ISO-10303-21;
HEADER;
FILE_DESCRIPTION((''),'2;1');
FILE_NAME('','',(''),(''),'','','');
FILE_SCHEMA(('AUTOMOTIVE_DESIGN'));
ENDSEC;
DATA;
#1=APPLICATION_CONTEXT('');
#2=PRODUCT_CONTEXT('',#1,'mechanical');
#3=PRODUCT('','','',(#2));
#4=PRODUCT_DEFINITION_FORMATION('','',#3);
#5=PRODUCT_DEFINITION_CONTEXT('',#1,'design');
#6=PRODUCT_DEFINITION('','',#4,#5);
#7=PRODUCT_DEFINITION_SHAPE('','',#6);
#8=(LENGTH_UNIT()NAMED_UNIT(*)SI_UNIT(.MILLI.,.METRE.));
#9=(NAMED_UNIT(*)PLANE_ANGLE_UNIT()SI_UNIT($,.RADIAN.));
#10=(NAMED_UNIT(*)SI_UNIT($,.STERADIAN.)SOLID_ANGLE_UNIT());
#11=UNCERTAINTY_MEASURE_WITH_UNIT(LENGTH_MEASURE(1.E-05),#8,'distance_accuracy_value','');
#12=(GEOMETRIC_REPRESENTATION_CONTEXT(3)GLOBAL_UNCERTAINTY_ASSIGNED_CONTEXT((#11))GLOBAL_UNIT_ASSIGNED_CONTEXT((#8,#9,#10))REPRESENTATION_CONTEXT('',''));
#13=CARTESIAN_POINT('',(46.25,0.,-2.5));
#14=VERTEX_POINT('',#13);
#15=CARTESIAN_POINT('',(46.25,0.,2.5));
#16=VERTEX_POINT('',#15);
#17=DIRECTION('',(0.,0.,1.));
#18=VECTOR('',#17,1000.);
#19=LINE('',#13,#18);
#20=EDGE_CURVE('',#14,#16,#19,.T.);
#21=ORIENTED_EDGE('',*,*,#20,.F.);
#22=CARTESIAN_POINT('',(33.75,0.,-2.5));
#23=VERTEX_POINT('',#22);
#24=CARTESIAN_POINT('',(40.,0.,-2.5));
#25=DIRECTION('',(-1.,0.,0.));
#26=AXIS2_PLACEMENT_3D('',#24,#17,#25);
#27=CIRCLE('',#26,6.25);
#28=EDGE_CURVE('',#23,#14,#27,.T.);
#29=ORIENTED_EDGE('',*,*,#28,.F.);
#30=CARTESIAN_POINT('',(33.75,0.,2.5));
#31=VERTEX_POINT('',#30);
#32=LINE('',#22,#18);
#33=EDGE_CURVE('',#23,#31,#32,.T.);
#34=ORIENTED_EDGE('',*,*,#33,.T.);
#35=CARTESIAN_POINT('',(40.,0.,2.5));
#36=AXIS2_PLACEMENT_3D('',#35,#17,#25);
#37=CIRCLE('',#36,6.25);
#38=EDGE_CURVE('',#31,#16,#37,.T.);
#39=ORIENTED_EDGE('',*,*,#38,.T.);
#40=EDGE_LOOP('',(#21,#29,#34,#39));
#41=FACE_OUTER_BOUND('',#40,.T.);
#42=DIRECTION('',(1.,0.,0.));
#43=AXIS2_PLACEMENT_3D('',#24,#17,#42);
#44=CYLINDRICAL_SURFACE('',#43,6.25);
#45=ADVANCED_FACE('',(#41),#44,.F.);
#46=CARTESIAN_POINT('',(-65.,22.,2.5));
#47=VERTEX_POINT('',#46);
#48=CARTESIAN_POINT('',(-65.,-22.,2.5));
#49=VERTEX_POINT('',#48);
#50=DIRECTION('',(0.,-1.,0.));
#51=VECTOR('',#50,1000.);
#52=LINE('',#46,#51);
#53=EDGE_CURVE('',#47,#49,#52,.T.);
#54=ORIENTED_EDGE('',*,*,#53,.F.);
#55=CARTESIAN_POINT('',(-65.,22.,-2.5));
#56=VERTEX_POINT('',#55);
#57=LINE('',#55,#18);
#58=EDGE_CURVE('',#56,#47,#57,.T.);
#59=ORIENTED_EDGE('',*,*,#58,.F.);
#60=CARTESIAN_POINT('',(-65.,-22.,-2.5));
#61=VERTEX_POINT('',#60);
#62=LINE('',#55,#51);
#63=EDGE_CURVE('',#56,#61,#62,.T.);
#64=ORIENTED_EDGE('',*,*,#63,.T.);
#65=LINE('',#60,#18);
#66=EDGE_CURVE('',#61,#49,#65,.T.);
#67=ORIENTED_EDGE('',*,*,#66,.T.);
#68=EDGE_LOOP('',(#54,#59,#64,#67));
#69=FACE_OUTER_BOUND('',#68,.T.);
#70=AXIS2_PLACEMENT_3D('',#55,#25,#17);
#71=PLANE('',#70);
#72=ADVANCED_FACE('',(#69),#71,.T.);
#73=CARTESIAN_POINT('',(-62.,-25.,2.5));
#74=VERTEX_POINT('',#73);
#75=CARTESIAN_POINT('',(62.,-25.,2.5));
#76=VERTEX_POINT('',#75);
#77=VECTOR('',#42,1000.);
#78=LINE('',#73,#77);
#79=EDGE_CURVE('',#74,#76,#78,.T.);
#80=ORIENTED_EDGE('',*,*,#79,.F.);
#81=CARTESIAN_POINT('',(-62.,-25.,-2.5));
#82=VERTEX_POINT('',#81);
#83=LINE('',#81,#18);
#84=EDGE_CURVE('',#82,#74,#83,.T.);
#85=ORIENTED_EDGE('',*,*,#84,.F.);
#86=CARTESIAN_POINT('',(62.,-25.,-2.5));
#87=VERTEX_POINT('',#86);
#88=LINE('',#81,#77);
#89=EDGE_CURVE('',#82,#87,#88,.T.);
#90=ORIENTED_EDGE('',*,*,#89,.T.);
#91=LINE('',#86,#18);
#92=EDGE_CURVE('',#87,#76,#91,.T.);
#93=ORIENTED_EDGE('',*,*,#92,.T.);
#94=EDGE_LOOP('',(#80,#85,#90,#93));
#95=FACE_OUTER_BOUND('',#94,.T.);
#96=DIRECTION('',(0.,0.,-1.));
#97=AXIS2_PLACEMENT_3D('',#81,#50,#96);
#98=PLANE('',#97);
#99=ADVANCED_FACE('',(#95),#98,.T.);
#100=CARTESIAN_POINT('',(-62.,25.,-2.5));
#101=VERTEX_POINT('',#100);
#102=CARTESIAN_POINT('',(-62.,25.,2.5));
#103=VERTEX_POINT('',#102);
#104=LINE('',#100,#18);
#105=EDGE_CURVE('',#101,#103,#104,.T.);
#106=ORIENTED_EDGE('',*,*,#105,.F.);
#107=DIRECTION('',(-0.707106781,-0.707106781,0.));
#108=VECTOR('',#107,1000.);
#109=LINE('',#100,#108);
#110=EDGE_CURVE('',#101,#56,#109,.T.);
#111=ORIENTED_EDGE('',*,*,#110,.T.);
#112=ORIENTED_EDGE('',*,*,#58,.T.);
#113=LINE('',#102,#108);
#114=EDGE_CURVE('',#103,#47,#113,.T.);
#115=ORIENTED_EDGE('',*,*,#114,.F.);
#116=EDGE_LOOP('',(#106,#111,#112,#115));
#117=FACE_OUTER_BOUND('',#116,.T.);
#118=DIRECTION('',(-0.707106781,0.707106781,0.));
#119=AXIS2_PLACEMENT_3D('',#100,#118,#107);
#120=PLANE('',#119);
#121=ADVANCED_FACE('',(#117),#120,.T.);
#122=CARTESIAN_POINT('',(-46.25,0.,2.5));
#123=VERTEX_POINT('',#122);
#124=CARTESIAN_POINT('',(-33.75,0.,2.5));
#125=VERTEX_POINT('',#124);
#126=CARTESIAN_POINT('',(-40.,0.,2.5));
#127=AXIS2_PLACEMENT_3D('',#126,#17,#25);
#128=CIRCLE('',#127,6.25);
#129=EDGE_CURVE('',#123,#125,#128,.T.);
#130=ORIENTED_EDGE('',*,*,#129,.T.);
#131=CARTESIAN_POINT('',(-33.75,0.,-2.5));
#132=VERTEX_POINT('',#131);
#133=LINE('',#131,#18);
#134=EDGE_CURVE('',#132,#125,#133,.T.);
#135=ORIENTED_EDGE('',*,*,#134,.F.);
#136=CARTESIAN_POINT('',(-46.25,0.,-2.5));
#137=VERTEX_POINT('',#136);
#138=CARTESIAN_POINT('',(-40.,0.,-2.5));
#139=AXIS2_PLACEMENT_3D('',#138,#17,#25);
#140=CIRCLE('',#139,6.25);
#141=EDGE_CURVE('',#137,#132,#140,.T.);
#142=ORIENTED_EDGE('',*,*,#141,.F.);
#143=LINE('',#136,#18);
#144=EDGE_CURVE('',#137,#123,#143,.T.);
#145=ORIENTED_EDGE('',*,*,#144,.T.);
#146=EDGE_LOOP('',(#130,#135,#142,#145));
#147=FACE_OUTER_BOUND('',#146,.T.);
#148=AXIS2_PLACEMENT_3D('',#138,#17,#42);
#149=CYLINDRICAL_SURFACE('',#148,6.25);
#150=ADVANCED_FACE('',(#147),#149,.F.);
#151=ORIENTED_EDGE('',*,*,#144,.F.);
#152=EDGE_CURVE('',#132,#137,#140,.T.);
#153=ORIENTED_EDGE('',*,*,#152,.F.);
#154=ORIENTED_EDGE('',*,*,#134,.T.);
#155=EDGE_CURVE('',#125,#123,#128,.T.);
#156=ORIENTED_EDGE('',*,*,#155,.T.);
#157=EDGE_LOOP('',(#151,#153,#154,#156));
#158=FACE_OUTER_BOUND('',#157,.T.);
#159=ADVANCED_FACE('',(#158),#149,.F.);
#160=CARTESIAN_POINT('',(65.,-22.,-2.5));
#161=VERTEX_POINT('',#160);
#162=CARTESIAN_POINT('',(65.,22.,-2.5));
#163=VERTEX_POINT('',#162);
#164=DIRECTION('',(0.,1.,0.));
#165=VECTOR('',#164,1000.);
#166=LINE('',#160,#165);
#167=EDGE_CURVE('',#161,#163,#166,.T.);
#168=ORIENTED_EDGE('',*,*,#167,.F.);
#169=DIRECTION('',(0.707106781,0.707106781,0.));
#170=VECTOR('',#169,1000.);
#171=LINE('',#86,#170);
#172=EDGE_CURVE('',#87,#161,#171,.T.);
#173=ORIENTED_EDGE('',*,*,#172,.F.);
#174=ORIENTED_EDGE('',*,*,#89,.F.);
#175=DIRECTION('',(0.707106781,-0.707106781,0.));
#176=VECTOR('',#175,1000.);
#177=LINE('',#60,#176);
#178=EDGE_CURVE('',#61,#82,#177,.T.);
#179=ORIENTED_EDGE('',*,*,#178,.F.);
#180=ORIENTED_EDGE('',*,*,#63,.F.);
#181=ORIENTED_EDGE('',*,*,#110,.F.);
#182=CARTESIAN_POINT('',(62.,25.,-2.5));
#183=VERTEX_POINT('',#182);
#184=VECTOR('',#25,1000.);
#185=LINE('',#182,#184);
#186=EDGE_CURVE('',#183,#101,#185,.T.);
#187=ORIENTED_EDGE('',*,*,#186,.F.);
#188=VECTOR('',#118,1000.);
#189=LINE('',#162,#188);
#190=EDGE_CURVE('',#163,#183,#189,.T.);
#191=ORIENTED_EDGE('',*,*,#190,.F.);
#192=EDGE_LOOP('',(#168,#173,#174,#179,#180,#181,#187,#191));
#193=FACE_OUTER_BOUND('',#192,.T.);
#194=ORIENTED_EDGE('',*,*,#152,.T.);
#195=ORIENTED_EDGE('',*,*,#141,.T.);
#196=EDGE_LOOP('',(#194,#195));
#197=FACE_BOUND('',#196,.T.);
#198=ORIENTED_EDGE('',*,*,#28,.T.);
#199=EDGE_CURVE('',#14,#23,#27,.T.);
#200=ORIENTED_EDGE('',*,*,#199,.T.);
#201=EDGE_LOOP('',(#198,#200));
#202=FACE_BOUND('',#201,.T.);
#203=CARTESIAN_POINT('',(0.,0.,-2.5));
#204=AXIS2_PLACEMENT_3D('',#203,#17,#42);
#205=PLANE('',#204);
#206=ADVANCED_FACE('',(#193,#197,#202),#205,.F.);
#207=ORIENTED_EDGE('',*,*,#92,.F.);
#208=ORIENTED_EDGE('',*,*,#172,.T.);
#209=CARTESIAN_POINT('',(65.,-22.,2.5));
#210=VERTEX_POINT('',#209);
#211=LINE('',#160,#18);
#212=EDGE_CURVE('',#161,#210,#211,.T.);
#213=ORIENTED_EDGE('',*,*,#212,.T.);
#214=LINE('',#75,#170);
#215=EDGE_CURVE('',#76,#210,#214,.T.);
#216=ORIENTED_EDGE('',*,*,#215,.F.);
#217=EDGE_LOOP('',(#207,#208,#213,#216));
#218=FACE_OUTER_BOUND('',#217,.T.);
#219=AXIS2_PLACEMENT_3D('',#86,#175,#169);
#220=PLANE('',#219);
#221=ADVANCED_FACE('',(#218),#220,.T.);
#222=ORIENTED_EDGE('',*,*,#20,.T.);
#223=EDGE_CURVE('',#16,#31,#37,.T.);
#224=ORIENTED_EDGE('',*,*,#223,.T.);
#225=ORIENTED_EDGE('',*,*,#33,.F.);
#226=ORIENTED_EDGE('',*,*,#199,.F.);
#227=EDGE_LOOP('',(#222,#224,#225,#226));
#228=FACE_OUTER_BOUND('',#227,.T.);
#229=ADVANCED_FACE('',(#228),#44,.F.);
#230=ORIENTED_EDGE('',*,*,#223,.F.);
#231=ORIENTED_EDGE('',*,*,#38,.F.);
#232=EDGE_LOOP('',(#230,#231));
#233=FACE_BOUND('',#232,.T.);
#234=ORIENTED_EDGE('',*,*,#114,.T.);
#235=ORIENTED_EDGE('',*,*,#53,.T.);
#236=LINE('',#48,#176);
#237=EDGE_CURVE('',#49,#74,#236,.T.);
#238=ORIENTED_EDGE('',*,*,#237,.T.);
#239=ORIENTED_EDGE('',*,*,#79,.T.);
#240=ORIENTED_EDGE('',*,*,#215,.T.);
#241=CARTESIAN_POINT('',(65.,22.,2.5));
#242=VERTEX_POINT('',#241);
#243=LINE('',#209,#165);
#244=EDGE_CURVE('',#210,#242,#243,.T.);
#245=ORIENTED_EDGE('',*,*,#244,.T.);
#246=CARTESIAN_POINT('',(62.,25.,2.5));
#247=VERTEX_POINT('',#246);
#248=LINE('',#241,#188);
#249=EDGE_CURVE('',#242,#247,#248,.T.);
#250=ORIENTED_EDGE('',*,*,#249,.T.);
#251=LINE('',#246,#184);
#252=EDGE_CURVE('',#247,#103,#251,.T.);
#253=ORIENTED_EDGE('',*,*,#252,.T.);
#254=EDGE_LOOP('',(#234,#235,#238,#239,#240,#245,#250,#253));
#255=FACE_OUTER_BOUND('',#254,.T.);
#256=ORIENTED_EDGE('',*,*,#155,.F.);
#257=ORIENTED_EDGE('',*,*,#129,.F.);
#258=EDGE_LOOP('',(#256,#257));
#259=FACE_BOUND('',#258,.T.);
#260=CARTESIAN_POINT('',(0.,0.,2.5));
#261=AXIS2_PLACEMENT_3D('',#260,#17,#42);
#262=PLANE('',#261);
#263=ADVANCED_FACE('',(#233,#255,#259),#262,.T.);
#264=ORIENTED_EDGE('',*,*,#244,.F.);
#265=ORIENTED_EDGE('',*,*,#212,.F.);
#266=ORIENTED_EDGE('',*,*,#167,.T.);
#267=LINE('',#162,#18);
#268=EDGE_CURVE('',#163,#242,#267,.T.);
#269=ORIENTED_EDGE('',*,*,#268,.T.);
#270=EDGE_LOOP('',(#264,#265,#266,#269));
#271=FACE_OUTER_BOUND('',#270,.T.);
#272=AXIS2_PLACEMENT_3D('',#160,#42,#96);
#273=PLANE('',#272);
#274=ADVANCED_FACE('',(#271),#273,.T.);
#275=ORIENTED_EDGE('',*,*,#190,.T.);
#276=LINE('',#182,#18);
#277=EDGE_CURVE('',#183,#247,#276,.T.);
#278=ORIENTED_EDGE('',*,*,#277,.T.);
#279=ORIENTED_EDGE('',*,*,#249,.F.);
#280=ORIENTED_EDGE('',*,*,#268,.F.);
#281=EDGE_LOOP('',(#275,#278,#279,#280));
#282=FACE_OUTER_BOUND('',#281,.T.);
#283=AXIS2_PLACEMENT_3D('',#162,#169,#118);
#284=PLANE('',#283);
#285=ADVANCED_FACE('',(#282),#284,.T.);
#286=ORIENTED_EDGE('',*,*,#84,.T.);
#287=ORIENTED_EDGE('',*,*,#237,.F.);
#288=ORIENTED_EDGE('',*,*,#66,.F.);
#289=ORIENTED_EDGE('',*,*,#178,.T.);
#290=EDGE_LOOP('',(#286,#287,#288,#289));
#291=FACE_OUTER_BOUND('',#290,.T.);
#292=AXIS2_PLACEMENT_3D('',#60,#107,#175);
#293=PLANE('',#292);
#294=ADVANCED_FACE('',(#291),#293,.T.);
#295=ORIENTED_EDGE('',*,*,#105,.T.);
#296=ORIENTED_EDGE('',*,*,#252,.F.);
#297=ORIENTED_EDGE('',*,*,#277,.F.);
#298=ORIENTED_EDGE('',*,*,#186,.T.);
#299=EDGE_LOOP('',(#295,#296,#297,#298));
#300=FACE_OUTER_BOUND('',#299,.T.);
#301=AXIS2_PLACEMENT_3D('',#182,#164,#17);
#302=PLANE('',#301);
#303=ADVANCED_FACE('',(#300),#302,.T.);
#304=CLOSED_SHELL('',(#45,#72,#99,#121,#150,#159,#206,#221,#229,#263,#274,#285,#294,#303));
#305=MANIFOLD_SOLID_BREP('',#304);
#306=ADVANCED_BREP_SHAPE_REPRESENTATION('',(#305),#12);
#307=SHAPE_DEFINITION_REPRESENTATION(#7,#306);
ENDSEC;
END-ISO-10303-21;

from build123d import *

# Parameters (mm, degrees)
SKETCH1_R           = 6.25
BOSS_EXTRUDE1_DEPTH = 5


with BuildPart() as part:
    # Sketch1 → Boss-Extrude1 (new body)
    with BuildSketch(Plane.XY.offset(2.5)):
        Polygon((-62, -25), (62, -25), (65, -22), (65, 22), (62, 25), (-62, 25), (-65, 22), (-65, -22), align=None)
        with Locations((-40, 0)):
            Circle(SKETCH1_R, mode=Mode.SUBTRACT)
        with Locations((40, 0)):
            Circle(SKETCH1_R, mode=Mode.SUBTRACT)
    extrude(amount=-BOSS_EXTRUDE1_DEPTH)


solid = part.part
